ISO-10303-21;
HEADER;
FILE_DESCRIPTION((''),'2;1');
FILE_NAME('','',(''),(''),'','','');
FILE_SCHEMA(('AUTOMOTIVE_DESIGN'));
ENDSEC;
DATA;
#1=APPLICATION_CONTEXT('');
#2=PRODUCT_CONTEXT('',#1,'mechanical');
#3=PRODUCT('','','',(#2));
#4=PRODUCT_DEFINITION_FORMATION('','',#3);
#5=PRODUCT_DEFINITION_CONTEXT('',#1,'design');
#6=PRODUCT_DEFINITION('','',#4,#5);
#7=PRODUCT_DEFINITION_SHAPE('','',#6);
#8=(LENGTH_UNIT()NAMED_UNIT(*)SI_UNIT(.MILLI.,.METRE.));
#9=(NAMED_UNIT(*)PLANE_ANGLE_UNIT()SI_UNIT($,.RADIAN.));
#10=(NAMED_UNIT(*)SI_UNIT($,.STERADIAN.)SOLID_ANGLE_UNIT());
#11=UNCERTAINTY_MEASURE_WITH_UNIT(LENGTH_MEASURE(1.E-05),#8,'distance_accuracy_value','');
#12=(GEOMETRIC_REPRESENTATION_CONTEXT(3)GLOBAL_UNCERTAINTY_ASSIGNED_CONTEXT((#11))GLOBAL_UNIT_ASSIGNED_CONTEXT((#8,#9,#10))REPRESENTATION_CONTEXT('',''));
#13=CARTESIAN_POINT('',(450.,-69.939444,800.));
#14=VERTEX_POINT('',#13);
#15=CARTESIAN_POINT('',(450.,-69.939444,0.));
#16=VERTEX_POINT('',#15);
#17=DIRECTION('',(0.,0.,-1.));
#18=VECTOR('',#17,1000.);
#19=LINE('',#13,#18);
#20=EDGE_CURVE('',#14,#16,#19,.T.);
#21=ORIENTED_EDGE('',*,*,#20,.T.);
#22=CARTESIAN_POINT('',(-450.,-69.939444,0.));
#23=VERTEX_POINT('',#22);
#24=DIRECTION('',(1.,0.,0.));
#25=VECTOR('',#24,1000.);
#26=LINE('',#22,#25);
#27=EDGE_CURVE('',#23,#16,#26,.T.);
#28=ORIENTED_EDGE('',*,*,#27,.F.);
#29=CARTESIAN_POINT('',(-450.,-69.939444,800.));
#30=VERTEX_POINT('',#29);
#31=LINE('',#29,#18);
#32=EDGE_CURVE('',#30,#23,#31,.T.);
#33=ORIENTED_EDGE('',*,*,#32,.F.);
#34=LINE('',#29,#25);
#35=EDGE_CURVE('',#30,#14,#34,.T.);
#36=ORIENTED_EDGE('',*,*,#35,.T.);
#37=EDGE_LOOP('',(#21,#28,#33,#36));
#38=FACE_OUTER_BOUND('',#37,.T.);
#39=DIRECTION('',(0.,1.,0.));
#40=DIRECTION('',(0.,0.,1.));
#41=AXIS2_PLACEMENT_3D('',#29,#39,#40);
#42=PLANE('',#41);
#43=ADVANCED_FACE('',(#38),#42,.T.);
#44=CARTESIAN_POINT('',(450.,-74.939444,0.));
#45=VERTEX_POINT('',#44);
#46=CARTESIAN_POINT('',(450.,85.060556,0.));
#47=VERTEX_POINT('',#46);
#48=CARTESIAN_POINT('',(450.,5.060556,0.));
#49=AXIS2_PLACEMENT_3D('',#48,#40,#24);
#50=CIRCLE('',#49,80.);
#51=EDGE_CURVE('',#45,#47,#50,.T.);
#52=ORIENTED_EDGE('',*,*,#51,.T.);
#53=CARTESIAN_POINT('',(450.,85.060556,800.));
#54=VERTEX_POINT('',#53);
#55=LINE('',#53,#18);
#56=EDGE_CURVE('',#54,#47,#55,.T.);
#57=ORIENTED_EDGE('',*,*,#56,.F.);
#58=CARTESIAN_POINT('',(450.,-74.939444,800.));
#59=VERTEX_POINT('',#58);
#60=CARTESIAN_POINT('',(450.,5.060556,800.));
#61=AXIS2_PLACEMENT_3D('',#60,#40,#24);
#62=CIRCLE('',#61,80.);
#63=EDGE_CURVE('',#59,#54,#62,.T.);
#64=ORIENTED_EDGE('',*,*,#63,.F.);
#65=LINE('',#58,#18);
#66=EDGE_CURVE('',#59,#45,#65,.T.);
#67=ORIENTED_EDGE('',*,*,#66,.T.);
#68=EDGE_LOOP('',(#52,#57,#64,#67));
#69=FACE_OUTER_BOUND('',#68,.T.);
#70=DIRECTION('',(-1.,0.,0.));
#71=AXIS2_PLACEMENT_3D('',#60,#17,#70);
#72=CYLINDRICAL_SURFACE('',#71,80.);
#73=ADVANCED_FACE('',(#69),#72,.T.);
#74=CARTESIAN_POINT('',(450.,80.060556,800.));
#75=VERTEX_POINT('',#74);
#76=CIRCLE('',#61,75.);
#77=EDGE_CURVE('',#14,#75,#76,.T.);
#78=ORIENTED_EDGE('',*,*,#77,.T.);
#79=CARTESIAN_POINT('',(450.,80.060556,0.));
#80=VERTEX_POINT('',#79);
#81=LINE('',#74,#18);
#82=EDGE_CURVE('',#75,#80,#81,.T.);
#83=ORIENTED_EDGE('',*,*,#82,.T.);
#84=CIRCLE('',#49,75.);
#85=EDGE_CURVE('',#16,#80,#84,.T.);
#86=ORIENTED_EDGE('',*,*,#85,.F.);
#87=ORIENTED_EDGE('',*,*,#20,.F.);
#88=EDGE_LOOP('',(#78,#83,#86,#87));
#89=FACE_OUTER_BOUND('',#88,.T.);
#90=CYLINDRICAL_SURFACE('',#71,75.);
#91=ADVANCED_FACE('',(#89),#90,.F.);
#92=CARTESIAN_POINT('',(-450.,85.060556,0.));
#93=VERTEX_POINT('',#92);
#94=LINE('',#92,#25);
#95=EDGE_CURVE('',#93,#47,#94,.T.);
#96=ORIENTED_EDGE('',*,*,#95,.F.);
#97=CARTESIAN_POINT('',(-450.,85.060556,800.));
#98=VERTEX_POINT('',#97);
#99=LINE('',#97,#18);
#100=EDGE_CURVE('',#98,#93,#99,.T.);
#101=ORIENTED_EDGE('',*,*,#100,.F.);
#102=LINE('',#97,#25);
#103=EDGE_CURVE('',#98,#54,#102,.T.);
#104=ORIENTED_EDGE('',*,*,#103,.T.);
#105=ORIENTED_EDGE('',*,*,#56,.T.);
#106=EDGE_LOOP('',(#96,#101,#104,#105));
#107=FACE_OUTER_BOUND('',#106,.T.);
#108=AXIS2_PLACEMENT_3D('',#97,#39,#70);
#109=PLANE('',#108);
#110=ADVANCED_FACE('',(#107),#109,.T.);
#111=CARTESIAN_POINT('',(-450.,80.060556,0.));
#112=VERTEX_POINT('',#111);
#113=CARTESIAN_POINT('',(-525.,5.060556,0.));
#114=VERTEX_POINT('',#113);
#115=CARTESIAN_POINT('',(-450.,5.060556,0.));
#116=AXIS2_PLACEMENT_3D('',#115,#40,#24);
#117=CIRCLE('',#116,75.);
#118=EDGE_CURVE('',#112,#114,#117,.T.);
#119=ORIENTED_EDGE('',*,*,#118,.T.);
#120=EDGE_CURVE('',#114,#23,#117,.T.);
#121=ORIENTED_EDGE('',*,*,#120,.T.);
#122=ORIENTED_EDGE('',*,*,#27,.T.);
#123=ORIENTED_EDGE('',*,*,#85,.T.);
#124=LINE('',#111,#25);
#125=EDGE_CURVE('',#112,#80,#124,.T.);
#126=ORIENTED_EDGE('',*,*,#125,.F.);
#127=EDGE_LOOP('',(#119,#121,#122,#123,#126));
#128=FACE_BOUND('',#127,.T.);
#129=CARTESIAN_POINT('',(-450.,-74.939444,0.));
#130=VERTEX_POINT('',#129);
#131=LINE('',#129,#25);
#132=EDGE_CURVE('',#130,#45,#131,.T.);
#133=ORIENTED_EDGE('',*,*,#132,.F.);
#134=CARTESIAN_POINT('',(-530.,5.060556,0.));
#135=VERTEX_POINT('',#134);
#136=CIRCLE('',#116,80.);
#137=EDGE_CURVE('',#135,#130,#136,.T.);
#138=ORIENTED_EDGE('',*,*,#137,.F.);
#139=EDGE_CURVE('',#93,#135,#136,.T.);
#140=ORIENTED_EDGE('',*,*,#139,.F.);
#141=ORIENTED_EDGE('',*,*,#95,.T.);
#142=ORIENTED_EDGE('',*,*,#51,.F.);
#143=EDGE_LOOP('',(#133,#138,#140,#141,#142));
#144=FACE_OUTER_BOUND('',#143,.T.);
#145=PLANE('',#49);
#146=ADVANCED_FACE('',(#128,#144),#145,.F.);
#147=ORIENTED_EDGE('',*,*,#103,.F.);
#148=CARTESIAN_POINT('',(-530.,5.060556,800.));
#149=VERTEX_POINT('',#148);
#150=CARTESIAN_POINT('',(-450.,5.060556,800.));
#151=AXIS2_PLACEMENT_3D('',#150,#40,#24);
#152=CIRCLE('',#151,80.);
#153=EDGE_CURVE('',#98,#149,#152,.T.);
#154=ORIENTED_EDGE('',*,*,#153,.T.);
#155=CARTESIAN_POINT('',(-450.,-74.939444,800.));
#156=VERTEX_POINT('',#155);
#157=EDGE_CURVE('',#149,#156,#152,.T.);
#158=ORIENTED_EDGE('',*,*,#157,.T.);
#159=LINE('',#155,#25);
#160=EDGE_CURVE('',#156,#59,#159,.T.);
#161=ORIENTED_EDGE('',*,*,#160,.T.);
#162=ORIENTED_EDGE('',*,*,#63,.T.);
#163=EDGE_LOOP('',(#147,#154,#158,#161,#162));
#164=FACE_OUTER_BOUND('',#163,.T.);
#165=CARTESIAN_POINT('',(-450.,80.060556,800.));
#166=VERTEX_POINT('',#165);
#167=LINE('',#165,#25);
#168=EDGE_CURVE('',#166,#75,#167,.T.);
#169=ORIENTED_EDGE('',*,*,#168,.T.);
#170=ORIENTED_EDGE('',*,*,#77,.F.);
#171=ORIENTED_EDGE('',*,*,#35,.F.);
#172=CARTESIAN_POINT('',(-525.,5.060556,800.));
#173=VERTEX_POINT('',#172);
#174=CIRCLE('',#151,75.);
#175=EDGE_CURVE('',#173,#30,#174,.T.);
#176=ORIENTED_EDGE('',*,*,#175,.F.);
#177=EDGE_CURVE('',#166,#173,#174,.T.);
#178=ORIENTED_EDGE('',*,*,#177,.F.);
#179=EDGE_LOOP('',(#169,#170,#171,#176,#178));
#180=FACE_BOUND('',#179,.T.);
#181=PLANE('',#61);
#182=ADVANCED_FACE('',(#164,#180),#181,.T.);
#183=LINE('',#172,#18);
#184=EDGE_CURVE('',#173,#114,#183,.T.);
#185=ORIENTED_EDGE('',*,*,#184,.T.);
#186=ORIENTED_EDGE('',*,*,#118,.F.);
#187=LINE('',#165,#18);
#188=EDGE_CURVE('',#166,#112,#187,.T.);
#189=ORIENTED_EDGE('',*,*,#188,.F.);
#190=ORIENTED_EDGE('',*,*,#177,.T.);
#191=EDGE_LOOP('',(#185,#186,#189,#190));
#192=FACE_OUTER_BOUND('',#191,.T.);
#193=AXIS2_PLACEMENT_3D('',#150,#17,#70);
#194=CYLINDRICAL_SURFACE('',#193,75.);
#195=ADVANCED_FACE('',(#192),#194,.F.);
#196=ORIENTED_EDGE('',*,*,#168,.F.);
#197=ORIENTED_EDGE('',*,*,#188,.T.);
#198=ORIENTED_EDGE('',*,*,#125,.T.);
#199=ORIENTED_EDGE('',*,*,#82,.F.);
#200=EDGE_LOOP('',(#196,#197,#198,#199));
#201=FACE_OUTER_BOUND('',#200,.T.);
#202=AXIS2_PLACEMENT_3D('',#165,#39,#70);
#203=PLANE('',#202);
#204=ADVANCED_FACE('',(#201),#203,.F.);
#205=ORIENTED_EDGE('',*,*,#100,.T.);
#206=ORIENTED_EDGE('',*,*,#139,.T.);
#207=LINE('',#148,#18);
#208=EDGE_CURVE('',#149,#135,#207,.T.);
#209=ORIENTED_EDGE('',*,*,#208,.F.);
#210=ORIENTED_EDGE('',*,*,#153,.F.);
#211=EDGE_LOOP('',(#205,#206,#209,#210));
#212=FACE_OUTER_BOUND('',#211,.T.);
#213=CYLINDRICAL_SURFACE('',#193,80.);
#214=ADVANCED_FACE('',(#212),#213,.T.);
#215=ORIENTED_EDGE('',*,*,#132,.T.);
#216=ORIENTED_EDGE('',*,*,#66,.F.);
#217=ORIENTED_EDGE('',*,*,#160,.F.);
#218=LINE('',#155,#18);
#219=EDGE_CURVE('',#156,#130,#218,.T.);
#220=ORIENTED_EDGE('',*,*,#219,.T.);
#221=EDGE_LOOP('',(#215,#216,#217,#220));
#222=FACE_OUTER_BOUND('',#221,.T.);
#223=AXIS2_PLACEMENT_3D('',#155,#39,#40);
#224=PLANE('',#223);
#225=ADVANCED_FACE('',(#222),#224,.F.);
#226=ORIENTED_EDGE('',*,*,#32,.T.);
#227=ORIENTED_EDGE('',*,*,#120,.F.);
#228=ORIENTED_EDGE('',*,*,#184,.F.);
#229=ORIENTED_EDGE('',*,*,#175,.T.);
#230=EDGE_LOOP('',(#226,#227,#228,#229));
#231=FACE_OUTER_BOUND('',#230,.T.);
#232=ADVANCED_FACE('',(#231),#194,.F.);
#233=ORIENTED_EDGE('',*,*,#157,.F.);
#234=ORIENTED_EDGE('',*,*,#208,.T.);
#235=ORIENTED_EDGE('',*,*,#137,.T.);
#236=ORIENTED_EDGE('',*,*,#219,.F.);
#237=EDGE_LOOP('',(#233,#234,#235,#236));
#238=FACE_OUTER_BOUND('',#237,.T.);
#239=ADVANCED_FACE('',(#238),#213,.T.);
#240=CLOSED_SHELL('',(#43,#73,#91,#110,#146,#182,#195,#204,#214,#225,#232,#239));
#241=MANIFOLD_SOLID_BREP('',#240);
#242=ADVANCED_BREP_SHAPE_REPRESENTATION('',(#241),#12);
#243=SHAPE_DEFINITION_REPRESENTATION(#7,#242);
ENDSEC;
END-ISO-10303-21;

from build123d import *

# Parameters (mm, degrees)
EXTRUDE_1_DEPTH = 800


with BuildPart() as part:
    # 草图1 → 拉伸-薄壁1 (new body)
    with BuildSketch(Plane.XY):
        with BuildLine():
            Line((450, -74.939443754), (-450, -74.939443754))
            ThreePointArc((-450, -74.939443754), (-530, 5.060556246), (-450, 85.060556246))
            Line((-450, 85.060556246), (450, 85.060556246))
            ThreePointArc((450, 85.060556246), (530, 5.060556246), (450, -74.939443754))
        make_face()
        with BuildLine():
            Line((450, -69.939443754), (-450, -69.939443754))
            ThreePointArc((-450, -69.939443754), (-525, 5.060556246), (-450, 80.060556246))
            Line((-450, 80.060556246), (450, 80.060556246))
            ThreePointArc((450, 80.060556246), (525, 5.060556246), (450, -69.939443754))
        make_face(mode=Mode.SUBTRACT)
    extrude(amount=EXTRUDE_1_DEPTH)


solid = part.part
